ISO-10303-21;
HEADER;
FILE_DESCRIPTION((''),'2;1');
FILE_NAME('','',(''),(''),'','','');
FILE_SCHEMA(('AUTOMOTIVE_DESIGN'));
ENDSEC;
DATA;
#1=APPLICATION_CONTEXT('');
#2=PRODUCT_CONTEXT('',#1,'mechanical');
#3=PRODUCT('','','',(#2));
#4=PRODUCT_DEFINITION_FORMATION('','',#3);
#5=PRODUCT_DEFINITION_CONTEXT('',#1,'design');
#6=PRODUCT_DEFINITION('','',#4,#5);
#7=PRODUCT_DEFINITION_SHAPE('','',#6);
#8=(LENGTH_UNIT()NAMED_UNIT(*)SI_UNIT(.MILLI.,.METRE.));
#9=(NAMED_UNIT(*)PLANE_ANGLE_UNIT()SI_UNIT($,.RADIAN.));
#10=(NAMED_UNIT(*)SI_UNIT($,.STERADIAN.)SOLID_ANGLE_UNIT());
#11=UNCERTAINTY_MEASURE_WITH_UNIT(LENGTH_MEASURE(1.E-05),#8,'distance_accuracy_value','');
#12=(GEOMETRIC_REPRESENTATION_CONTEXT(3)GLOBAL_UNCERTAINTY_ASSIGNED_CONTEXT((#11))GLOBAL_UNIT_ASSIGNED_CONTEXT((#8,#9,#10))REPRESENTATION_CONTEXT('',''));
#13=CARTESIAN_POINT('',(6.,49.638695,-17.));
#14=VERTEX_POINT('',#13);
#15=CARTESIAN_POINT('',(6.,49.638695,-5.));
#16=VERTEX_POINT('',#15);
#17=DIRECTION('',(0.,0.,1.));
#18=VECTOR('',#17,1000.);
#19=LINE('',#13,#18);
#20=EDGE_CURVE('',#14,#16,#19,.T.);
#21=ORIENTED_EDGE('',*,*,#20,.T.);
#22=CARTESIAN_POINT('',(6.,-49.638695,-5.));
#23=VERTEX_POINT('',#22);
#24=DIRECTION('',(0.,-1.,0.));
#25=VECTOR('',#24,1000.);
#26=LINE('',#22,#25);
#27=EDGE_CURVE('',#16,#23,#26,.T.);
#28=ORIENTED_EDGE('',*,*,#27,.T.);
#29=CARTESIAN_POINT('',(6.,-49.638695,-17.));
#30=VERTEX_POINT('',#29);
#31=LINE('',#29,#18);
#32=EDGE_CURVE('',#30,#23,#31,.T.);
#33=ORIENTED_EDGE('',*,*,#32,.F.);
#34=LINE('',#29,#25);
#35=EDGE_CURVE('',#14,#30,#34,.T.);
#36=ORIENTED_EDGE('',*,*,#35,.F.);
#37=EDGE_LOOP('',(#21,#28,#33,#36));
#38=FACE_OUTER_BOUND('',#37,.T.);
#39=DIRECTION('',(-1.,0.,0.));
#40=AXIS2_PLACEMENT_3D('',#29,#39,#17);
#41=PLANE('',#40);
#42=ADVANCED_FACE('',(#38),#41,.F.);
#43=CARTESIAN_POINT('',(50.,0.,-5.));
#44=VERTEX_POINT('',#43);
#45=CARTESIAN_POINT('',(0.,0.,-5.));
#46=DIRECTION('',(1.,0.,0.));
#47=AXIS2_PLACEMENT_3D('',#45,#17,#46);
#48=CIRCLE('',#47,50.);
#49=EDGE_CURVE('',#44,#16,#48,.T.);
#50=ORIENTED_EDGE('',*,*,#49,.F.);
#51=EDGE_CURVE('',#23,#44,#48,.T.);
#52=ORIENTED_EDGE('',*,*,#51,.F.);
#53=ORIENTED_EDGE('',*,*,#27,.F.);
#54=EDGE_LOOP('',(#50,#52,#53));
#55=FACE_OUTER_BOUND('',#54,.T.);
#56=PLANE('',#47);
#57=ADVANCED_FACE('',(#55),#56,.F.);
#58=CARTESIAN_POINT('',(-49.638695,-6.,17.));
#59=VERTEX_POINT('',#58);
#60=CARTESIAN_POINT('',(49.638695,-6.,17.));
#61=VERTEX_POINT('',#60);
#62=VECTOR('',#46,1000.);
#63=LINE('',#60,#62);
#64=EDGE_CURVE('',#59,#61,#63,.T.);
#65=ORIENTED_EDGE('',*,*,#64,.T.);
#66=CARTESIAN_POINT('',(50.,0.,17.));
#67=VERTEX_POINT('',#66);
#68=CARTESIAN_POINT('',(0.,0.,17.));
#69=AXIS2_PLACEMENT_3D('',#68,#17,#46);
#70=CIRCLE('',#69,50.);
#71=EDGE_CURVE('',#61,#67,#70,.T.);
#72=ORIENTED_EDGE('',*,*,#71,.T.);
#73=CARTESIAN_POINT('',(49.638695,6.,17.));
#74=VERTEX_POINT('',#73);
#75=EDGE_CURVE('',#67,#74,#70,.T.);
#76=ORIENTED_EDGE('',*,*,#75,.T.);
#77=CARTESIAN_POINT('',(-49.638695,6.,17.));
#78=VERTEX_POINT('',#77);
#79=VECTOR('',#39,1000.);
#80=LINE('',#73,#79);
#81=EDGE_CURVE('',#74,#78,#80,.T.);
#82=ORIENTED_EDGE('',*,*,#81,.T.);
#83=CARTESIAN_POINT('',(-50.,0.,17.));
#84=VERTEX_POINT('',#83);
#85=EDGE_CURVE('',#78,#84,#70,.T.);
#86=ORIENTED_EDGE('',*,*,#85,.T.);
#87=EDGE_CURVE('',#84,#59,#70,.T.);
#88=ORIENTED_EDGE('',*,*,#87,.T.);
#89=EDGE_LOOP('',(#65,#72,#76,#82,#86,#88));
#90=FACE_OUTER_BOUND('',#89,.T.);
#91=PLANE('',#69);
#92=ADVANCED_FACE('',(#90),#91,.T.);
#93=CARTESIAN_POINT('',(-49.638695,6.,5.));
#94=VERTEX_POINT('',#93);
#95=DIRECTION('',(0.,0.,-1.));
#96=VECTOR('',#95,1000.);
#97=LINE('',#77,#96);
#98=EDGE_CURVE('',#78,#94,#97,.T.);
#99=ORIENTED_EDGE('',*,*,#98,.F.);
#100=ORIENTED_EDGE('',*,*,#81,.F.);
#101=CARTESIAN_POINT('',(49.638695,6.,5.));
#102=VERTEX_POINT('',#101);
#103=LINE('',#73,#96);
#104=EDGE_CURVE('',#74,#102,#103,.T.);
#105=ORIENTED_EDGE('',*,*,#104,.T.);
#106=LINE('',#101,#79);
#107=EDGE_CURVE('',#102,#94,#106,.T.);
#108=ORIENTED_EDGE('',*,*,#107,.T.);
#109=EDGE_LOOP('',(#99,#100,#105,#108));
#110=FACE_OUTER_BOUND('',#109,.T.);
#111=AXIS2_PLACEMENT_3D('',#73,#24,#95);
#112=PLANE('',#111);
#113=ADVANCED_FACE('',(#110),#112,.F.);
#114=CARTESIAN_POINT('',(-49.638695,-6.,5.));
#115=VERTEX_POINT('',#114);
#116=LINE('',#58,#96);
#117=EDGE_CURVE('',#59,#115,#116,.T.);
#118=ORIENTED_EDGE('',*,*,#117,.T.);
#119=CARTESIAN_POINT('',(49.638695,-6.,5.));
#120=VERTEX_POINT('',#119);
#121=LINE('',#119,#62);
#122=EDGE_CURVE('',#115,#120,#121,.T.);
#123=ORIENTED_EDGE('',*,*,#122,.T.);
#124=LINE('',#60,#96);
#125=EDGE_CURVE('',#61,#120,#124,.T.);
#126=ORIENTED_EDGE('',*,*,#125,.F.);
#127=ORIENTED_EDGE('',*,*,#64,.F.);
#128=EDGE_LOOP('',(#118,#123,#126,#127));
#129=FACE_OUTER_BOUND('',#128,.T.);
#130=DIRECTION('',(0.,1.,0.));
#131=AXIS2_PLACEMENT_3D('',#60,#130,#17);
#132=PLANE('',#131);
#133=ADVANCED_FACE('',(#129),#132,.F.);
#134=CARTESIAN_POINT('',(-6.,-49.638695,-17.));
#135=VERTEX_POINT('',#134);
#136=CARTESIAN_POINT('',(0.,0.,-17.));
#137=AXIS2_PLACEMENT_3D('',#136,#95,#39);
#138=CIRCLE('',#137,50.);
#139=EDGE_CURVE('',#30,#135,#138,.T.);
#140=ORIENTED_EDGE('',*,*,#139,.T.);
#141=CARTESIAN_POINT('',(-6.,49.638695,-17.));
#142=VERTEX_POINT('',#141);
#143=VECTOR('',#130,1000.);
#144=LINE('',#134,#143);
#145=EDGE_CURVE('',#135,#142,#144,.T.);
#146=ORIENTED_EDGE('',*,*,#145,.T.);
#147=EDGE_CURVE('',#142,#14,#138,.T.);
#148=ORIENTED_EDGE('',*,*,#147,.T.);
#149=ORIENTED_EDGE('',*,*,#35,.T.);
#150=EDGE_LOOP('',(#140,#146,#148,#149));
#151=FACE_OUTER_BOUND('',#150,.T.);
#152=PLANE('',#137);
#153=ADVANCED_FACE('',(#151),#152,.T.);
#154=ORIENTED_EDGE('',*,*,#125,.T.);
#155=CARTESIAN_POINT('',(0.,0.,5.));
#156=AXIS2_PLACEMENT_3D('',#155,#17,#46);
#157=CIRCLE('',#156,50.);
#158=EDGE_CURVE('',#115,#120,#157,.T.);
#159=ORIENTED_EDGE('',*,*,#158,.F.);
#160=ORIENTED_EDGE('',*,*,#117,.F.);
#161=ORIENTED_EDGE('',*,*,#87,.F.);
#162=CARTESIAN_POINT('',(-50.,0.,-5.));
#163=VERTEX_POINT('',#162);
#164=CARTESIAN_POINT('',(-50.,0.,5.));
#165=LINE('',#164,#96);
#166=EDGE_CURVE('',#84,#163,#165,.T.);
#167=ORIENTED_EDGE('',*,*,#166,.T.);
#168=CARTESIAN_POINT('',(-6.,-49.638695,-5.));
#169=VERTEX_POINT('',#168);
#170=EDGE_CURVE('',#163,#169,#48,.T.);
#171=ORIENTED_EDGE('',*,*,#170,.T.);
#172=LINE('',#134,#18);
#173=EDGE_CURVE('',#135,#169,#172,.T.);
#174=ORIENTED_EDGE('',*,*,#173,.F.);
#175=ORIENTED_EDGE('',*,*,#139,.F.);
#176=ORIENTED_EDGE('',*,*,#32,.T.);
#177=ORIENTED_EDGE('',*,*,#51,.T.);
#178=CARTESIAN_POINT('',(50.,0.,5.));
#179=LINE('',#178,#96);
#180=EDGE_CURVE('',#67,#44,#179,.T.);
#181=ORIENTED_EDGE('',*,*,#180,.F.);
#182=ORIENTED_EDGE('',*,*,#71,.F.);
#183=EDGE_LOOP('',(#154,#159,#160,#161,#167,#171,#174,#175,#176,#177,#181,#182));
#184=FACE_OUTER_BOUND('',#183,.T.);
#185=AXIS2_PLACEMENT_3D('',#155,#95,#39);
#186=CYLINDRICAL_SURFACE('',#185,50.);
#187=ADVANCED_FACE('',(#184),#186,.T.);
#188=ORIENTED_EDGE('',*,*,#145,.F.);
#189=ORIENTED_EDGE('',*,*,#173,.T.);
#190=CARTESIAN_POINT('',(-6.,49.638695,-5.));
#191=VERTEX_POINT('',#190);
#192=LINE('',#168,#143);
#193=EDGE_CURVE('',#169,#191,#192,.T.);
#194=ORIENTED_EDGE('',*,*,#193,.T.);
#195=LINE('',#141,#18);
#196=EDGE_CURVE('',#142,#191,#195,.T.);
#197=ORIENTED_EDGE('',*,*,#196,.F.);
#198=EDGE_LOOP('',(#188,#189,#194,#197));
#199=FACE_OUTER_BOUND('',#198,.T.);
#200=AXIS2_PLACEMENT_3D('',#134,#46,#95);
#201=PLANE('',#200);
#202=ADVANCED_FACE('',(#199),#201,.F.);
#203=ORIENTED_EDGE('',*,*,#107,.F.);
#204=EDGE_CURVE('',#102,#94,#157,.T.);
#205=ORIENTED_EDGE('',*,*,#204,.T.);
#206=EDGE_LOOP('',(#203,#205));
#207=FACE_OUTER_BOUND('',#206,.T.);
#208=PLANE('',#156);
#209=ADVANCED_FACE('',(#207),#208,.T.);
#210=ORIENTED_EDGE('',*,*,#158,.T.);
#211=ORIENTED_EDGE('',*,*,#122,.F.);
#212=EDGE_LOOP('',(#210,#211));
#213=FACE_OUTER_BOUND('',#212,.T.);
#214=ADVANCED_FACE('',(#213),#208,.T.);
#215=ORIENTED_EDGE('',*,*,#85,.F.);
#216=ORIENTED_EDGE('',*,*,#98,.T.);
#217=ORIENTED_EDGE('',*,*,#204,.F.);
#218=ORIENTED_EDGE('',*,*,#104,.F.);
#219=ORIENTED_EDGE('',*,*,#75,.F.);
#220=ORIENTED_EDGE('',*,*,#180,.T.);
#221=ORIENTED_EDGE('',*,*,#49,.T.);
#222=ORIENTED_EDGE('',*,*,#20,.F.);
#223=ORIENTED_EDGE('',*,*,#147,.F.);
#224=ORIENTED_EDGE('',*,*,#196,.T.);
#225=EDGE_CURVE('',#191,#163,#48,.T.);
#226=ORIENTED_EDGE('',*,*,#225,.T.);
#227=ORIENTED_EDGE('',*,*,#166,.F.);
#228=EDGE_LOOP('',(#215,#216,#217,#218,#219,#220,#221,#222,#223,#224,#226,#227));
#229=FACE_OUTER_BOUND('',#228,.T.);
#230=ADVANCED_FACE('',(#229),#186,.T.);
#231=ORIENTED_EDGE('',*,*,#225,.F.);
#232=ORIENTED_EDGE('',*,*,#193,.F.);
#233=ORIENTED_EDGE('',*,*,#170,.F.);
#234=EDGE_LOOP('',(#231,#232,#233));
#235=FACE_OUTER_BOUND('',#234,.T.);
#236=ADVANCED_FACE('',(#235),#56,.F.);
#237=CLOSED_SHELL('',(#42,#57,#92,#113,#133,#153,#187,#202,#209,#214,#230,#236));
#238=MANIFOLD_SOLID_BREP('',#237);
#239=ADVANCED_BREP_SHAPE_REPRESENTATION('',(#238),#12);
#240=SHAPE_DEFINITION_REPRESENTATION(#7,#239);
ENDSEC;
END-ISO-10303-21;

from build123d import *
from build123d.topology import SkipClean

# Parameters (mm, degrees)
DISC_PROFILE_100_R = 50
DISC_BODY_DEPTH    = 5
FACE_START         = 12
FACE_RIB_1_DEPTH   = 12
FACE_RIB_2_DEPTH   = 12


with BuildPart() as part:
    # Disc Profile Ø100 → Disc Body (new, symmetric)
    with BuildSketch(Plane.XY):
        Circle(DISC_PROFILE_100_R)
    extrude(amount=DISC_BODY_DEPTH, both=True)

    # Face Rib 1 Profile → Face Rib 1 (add)
    with SkipClean():  # the faces are left unmerged after this step: merging them gives an invalid solid
        with BuildSketch(Plane.XY.offset(5).offset(FACE_START)):
            with BuildLine():
                Line((49.638694584, -6), (-49.638694584, -6))
                ThreePointArc((-49.638694584, -6), (-50, 0), (-49.638694584, 6))
                Line((-49.638694584, 6), (49.638694584, 6))
                ThreePointArc((49.638694584, 6), (50, 0), (49.638694584, -6))
            make_face()
        extrude(amount=-FACE_RIB_1_DEPTH)

    # Face Rib 2 Profile → Face Rib 2 (add)
    with SkipClean():  # the faces are left unmerged after this step: merging them gives an invalid solid
        with BuildSketch(Plane(origin=(0, 0, -5), x_dir=(-1, 0, 0), z_dir=(0, 0, -1))):
            with BuildLine():
                Line((-6, -49.638694584), (-6, 49.638694584))
                ThreePointArc((-6, 49.638694584), (0, 50), (6, 49.638694584))
                Line((6, 49.638694584), (6, -49.638694584))
                ThreePointArc((6, -49.638694584), (0, -50), (-6, -49.638694584))
            make_face()
        extrude(amount=FACE_RIB_2_DEPTH)


solid = part.part
